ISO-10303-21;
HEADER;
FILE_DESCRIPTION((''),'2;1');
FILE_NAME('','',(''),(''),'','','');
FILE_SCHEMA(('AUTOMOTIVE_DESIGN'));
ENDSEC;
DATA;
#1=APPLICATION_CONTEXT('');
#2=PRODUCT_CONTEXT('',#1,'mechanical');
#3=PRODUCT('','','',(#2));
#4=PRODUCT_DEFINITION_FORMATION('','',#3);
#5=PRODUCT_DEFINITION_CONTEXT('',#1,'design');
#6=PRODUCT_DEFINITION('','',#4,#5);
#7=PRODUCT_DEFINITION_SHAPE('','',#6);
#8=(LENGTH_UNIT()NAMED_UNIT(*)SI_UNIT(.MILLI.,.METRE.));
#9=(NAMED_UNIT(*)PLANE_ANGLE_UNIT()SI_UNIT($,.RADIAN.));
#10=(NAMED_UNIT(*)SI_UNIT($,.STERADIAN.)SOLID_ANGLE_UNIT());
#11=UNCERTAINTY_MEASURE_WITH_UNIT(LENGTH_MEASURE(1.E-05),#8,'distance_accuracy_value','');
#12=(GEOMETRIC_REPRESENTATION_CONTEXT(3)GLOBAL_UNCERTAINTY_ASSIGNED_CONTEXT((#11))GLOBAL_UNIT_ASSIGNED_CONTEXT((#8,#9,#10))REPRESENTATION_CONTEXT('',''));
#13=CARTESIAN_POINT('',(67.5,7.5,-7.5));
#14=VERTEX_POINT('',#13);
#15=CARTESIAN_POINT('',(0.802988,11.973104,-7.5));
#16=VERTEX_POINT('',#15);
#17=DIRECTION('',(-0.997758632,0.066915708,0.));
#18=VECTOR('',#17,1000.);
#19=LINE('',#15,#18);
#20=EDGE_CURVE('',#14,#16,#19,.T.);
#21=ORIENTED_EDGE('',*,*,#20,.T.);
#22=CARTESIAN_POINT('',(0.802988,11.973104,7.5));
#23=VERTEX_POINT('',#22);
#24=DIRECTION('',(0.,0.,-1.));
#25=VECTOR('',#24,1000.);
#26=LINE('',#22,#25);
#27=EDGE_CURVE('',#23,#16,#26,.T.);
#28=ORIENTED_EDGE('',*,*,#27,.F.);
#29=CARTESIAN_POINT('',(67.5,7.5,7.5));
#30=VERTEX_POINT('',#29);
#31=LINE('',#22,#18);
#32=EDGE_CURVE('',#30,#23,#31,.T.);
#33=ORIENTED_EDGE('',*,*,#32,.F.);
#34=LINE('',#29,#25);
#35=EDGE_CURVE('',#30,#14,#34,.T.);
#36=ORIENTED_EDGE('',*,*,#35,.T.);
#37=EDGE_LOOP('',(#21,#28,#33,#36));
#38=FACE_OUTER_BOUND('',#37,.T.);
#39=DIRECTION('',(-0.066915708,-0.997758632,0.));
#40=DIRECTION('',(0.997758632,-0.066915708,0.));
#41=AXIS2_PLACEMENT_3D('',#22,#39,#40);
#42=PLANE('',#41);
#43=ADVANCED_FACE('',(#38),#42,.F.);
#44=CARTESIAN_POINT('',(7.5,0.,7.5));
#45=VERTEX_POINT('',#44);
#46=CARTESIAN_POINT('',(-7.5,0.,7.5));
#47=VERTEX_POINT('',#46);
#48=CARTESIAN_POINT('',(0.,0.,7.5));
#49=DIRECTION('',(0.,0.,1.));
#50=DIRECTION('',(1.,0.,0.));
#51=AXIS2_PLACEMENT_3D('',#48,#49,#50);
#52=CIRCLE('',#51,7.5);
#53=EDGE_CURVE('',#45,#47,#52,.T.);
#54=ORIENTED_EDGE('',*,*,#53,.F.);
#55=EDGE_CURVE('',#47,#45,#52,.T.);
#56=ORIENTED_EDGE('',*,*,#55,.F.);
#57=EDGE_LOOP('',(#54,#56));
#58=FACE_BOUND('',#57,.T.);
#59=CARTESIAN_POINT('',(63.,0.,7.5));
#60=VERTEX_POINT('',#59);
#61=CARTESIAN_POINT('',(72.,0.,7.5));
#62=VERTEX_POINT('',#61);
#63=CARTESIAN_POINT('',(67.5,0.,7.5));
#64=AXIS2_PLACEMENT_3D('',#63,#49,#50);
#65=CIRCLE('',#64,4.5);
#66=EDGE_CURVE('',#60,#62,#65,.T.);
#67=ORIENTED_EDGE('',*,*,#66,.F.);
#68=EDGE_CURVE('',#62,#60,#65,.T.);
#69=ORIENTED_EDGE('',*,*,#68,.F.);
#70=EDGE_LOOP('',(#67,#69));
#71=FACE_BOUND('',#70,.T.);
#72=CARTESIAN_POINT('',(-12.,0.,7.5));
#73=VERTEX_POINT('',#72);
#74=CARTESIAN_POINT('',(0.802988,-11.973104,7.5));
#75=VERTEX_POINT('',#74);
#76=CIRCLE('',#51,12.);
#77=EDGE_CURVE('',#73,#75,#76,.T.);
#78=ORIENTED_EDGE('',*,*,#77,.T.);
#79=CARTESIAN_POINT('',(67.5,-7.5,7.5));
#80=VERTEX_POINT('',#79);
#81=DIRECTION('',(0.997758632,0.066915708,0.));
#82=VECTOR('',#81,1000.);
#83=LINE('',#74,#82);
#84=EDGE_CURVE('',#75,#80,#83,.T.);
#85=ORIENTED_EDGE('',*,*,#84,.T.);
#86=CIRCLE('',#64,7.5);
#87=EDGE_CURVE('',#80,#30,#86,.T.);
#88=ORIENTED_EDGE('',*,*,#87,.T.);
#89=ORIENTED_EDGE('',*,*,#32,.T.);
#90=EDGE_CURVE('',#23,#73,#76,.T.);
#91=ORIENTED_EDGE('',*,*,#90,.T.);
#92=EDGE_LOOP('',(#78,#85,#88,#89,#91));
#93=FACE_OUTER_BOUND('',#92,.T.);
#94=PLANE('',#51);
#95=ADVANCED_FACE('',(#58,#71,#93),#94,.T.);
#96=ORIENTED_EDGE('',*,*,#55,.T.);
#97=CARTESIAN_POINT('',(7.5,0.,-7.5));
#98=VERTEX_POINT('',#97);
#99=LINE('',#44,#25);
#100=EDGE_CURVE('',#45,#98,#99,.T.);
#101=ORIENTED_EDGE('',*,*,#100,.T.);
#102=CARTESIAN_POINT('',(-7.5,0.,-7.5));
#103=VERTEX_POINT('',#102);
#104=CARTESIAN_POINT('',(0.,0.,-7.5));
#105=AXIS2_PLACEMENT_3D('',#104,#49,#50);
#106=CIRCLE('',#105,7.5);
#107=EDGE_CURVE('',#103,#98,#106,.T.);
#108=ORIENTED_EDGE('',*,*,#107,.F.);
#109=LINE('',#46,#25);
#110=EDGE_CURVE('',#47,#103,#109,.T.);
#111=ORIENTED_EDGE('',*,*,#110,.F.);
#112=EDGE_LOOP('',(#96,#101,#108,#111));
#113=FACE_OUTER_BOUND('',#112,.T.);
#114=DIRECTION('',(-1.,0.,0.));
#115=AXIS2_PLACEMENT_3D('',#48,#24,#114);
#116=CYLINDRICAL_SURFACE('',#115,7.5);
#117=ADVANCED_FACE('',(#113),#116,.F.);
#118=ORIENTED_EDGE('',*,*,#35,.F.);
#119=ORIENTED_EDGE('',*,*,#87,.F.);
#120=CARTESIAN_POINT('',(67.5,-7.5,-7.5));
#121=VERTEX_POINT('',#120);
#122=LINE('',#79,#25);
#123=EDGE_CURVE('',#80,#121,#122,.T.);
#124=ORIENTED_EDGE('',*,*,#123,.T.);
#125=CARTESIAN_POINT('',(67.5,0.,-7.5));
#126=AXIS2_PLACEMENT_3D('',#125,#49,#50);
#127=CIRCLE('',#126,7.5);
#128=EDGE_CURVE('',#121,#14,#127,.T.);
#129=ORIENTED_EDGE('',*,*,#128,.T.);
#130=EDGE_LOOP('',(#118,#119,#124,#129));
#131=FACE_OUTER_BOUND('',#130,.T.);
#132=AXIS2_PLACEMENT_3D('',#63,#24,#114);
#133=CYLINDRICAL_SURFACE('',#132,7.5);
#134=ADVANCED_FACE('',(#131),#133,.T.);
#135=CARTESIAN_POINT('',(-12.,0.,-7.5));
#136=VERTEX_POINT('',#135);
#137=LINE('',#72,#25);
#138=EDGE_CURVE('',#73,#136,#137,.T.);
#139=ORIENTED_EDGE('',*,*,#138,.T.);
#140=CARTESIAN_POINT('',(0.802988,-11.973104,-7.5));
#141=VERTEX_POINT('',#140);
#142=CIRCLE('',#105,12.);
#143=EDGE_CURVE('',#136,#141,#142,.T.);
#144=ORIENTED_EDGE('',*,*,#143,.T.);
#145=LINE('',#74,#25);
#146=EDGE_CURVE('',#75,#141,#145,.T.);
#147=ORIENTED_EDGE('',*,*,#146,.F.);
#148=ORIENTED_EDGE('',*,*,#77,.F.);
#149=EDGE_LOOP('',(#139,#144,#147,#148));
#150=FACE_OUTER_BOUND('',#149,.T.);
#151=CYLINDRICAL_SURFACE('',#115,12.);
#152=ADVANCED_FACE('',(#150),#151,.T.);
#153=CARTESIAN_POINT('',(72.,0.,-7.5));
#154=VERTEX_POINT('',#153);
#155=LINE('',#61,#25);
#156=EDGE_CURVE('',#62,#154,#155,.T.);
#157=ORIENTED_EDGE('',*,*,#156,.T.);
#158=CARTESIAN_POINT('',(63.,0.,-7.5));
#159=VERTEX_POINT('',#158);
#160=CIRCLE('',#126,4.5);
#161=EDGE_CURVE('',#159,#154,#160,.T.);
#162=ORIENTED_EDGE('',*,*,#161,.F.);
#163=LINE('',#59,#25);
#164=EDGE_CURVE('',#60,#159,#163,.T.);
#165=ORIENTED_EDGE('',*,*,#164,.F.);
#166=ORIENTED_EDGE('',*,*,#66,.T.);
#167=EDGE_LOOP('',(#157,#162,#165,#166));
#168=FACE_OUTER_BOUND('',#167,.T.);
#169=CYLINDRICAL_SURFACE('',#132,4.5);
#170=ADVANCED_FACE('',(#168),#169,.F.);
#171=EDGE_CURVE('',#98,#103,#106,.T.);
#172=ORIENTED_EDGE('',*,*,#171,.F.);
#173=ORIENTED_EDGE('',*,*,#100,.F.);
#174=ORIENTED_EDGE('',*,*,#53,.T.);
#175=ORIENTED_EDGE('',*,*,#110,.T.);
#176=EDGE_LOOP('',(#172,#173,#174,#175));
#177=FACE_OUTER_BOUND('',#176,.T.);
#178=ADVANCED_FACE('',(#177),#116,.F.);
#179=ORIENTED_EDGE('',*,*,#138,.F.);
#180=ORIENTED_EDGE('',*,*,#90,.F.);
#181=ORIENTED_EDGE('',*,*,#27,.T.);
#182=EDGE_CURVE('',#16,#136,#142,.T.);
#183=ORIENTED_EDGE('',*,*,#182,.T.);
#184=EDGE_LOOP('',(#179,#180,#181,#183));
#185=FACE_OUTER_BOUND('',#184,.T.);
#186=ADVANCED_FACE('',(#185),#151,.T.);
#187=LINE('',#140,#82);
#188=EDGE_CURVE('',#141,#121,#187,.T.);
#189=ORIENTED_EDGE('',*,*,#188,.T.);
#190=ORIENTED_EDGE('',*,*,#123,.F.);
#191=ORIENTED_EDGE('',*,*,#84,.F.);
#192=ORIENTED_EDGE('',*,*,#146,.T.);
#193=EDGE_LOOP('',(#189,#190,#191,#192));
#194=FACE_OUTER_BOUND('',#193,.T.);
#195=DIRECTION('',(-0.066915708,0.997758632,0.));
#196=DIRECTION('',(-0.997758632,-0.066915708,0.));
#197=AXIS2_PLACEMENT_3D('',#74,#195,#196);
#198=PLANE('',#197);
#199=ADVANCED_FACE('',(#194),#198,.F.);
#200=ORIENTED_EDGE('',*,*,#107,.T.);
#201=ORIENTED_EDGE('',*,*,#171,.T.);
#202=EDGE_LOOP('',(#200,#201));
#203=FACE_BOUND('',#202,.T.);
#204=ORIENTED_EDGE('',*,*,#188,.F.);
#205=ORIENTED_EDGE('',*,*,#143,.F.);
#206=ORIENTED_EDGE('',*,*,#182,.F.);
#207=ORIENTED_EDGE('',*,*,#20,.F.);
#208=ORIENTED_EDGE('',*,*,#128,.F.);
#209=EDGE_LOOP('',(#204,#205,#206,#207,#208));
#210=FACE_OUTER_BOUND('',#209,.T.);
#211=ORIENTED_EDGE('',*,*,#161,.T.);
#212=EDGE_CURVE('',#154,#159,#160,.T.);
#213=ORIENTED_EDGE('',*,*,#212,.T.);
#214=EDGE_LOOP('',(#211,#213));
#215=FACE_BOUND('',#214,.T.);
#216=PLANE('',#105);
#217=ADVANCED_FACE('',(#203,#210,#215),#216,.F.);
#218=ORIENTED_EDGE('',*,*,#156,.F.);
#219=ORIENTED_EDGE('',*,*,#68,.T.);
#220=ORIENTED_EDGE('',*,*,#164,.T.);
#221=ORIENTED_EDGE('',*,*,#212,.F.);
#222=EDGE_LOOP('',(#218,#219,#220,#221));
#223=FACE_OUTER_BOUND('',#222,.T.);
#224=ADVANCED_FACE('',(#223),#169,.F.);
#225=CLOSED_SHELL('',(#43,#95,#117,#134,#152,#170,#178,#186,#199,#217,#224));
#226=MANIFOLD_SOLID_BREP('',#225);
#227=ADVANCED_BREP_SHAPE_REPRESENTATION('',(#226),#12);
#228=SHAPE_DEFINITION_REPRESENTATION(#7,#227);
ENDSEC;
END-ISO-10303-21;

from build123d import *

# Parameters (mm, degrees)
SKETCH1_R           = 7.5
SKETCH1_R_2         = 4.5
BOSS_EXTRUDE1_DEPTH = 7.5


with BuildPart() as part:
    # Sketch1 → Boss-Extrude1 (new, symmetric)
    with BuildSketch(Plane.XY):
        with BuildLine():
            Line((0.80298849, 11.973103586), (67.5, 7.5))
            ThreePointArc((67.5, 7.5), (75, 0), (67.5, -7.5))
            Line((67.5, -7.5), (0.80298849, -11.973103586))
            ThreePointArc((0.80298849, -11.973103586), (-12, 0), (0.80298849, 11.973103586))
        make_face()
        Circle(SKETCH1_R, mode=Mode.SUBTRACT)
        with Locations((67.5, 0)):
            Circle(SKETCH1_R_2, mode=Mode.SUBTRACT)
    extrude(amount=BOSS_EXTRUDE1_DEPTH, both=True)


solid = part.part
